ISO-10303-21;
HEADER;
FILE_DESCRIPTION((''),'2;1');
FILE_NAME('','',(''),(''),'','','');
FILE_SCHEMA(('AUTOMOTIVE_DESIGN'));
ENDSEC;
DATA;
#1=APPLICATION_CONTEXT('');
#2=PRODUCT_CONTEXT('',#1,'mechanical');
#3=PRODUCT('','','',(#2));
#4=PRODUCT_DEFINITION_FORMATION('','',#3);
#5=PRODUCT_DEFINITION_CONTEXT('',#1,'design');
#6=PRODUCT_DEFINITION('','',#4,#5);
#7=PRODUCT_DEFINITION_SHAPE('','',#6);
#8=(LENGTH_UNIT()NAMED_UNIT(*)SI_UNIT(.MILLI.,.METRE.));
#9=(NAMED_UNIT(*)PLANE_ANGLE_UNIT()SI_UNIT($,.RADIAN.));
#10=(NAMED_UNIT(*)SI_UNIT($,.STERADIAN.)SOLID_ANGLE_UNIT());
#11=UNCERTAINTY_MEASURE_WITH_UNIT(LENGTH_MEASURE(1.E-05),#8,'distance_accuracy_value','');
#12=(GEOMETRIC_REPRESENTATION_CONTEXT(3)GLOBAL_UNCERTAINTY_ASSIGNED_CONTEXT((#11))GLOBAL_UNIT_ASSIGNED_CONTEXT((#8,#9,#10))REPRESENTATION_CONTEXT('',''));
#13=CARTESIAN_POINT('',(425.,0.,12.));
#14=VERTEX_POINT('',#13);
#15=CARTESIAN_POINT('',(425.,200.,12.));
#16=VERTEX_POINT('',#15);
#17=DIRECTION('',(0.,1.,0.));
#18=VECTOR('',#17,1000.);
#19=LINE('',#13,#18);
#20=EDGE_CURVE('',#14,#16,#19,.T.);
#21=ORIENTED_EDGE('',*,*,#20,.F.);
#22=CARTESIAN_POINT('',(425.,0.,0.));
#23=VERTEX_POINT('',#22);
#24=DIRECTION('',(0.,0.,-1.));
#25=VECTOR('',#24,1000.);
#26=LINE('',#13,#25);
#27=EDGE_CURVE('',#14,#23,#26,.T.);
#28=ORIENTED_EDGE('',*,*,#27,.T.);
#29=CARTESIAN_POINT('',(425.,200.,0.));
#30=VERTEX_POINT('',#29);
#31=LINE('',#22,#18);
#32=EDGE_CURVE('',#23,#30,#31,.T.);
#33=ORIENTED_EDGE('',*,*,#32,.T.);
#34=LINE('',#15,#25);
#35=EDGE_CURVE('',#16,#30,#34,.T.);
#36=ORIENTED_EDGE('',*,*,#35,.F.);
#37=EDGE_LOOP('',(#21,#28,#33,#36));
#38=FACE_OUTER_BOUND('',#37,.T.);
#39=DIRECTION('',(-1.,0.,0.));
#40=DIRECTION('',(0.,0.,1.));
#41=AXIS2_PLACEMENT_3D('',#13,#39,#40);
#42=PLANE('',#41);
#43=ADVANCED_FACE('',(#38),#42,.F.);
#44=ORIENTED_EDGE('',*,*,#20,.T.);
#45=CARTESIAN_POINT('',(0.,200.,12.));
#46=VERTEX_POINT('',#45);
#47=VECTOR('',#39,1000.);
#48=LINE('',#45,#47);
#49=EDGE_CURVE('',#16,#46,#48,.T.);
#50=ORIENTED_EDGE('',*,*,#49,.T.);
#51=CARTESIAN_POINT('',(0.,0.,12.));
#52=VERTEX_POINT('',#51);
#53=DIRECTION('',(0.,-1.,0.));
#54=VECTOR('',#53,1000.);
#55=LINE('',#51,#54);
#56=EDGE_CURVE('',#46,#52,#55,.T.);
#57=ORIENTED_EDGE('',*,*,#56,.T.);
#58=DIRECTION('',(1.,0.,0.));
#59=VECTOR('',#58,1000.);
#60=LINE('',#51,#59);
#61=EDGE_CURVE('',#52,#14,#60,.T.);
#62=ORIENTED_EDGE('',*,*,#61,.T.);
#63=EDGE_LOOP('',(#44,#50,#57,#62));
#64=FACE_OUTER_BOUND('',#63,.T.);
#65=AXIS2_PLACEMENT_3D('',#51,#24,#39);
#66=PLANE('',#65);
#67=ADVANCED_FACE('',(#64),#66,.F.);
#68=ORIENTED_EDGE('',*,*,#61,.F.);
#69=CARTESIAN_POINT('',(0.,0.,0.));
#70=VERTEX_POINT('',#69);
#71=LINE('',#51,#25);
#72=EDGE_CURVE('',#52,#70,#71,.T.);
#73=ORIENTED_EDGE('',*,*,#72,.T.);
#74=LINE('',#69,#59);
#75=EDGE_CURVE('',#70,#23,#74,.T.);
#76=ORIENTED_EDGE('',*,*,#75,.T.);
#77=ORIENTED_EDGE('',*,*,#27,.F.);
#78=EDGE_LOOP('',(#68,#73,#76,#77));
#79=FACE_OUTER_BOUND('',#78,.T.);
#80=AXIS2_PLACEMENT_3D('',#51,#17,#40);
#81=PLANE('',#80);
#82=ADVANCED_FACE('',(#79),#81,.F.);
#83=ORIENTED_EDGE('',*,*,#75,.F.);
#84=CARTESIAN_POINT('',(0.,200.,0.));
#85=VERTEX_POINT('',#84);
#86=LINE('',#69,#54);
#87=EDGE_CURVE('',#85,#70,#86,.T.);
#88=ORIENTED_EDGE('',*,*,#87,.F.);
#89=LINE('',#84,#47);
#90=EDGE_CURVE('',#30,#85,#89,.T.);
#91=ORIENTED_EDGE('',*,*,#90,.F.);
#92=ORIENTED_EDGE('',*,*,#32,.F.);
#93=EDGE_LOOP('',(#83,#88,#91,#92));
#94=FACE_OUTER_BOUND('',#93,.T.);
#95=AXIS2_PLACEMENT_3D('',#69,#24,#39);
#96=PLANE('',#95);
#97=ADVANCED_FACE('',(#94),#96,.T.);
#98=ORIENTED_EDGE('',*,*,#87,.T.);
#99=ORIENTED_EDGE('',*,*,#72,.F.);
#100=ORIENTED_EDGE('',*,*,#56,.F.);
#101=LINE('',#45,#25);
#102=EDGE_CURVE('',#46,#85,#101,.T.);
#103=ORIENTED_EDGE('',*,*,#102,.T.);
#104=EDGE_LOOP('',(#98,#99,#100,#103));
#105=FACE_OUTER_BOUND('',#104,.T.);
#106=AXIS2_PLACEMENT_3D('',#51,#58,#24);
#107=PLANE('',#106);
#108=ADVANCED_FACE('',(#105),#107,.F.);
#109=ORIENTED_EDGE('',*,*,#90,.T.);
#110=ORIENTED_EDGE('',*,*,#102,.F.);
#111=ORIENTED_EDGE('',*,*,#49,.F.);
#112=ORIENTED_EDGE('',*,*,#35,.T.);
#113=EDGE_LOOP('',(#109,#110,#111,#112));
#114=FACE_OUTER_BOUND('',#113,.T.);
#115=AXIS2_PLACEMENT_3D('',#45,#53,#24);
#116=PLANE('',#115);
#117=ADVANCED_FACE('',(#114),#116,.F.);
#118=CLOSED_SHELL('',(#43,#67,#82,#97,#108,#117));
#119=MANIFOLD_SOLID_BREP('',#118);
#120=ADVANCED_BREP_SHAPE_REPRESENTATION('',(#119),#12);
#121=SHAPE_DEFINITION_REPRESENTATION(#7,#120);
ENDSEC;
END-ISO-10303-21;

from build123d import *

# Parameters (mm, degrees)
SKETCH1_W           = 425
SKETCH1_H           = 200
BOSS_EXTRUDE1_DEPTH = 12


with BuildPart() as part:
    # Sketch1 → Boss-Extrude1 (new body)
    with BuildSketch(Plane.XY):
        with Locations((212.5, 100)):
            Rectangle(SKETCH1_W, SKETCH1_H)
    extrude(amount=BOSS_EXTRUDE1_DEPTH)


solid = part.part
